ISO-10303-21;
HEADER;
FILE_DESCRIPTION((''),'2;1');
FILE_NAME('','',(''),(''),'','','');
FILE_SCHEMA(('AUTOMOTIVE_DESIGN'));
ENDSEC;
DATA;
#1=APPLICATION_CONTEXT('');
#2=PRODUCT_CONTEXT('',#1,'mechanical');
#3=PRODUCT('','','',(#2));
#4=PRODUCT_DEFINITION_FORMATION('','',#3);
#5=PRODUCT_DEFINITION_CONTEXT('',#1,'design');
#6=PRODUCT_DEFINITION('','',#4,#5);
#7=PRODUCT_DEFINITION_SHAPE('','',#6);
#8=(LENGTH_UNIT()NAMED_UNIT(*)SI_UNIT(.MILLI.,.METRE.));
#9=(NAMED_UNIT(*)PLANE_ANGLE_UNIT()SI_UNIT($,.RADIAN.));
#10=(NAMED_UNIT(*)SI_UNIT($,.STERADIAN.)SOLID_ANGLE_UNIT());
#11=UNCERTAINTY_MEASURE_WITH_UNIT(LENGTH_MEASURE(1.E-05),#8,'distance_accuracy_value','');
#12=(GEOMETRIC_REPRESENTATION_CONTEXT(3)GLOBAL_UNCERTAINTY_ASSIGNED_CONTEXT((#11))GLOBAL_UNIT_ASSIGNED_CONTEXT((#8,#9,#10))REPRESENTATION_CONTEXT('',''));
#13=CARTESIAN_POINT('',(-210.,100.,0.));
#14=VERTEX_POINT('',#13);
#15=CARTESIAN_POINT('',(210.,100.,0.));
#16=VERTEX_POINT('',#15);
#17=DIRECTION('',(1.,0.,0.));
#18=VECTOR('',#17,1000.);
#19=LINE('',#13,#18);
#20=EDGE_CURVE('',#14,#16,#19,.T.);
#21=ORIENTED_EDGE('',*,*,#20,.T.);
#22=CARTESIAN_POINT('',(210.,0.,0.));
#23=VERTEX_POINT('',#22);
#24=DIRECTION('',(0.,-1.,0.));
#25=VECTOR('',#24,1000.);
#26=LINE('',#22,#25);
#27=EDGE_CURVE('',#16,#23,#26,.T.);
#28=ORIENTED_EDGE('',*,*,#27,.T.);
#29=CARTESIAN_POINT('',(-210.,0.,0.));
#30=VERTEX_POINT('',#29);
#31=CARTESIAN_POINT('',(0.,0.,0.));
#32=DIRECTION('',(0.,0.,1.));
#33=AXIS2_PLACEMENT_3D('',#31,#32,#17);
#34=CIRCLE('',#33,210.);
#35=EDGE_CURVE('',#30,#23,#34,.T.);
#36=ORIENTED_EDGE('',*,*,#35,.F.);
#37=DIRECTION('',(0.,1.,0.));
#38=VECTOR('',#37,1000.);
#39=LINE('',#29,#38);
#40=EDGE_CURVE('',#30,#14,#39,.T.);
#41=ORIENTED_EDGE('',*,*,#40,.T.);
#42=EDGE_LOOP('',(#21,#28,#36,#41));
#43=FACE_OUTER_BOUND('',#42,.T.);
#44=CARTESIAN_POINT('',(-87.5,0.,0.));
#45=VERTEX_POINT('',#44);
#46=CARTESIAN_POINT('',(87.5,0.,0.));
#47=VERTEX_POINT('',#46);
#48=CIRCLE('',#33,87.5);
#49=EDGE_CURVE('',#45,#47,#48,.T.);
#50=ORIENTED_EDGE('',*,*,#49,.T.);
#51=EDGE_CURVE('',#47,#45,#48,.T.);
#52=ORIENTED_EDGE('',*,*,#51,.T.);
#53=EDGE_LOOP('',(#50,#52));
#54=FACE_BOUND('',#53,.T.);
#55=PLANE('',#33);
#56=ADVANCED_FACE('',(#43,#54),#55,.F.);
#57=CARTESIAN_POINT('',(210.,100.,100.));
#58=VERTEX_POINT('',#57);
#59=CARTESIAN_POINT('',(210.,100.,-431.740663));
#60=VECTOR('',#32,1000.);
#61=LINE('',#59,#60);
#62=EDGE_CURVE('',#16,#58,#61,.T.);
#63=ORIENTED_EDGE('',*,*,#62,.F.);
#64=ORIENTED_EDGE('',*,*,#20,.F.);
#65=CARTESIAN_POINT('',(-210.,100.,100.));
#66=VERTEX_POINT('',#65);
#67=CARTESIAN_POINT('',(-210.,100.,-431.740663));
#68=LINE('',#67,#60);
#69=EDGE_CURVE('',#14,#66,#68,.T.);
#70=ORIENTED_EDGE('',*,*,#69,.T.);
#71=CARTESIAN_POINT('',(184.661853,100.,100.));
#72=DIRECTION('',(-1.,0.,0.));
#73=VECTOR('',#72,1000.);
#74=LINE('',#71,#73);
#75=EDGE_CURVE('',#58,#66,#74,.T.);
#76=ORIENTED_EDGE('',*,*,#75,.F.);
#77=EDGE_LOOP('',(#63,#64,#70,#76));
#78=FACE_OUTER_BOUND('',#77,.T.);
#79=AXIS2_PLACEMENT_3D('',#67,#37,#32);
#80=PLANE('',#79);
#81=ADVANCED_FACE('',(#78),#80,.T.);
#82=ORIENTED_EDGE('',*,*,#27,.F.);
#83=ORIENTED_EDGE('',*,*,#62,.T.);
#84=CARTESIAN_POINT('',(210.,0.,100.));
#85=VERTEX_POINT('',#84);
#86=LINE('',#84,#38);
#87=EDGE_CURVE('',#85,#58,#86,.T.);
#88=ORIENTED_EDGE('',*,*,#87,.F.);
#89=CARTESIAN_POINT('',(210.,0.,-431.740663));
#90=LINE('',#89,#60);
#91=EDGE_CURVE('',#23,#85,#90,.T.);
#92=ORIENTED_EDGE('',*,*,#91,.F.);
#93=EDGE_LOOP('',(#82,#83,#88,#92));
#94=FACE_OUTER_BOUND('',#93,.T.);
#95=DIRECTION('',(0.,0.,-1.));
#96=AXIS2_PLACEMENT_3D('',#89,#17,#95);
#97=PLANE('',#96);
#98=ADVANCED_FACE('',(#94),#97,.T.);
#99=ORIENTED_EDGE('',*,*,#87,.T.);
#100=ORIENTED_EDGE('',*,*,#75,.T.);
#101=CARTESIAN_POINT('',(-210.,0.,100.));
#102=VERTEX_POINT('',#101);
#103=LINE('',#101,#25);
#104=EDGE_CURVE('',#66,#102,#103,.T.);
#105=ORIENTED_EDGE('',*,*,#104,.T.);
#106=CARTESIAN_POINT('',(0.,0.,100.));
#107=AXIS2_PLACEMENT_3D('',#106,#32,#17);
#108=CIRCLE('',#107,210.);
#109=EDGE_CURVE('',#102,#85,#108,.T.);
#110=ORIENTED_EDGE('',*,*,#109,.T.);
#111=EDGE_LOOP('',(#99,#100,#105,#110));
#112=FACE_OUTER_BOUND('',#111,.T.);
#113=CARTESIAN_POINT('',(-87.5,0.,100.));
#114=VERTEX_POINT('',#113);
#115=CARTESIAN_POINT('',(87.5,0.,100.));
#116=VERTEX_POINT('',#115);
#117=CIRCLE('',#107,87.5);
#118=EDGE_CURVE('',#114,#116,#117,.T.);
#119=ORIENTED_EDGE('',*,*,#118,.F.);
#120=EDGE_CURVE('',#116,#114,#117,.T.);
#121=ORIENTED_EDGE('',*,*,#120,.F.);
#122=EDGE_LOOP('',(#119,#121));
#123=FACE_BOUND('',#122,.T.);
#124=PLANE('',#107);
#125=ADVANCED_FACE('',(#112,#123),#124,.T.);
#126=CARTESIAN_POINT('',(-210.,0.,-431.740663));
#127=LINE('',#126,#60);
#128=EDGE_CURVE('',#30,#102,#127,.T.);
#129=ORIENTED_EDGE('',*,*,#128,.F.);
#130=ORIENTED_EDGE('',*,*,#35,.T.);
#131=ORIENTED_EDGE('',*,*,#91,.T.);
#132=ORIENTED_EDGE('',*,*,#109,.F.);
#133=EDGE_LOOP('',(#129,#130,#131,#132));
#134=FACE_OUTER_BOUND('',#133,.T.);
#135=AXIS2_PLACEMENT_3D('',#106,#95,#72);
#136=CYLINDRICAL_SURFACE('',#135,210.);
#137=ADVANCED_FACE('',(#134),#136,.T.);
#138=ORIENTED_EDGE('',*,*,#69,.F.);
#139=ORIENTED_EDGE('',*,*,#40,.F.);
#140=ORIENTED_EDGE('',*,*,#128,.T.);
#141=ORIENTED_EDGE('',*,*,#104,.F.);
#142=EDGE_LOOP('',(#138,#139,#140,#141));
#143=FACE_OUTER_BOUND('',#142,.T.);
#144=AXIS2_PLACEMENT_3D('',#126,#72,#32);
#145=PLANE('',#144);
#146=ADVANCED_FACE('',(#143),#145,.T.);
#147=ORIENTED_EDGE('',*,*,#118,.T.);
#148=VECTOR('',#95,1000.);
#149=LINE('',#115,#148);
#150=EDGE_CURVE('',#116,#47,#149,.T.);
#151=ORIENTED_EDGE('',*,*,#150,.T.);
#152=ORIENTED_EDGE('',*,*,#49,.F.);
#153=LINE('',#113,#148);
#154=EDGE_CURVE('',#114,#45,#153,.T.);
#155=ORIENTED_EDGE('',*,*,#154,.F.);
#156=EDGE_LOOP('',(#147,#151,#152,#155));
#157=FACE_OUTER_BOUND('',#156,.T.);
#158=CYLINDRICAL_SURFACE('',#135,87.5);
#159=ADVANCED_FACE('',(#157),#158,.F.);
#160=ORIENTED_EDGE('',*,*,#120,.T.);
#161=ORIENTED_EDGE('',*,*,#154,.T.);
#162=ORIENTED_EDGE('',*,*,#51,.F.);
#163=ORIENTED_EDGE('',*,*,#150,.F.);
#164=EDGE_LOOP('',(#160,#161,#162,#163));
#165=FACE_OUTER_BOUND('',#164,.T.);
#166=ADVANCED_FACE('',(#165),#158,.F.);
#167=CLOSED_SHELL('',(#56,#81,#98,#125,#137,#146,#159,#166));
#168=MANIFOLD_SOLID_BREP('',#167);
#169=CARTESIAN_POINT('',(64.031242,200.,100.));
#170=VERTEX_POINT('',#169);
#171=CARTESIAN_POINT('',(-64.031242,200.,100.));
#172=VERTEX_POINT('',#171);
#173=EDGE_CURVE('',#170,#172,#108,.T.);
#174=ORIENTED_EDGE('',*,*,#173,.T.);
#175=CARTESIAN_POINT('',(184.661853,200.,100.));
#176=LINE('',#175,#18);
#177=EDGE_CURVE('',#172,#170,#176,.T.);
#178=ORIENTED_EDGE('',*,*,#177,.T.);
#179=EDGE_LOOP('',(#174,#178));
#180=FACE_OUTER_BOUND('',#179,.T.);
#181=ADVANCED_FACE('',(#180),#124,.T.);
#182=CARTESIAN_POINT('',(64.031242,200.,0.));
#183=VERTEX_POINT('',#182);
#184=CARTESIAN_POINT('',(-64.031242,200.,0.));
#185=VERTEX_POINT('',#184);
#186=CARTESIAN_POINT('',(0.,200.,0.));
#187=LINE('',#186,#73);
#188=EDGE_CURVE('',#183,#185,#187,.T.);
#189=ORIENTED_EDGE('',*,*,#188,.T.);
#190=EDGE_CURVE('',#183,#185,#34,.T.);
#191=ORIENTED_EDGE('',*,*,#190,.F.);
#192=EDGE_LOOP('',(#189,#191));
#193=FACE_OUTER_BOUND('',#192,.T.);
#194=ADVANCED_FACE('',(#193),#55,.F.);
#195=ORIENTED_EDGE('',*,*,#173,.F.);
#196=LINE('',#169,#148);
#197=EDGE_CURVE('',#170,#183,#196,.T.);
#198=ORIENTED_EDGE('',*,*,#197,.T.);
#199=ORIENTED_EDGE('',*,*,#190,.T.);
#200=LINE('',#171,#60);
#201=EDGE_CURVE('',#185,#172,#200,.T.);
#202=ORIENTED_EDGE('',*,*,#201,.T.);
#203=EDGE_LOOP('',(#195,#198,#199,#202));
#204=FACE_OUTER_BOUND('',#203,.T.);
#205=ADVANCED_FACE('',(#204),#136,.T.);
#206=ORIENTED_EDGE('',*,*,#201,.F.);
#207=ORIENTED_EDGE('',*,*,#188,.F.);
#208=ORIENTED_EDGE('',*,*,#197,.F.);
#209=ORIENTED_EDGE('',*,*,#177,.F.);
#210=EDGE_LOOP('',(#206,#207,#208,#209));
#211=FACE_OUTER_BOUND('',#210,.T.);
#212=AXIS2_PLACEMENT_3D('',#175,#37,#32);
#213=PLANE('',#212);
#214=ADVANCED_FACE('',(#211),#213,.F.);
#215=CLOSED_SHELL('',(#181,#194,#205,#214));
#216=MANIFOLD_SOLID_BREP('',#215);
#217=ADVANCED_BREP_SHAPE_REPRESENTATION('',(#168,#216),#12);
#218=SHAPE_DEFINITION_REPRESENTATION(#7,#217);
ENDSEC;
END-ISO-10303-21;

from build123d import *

# Parameters (mm, degrees)
SKETCH1_R           = 210
SKETCH1_R_2         = 87.5
BOSS_EXTRUDE1_DEPTH = 100
BOSS_EXTRUDE2_START = -100
BOSS_EXTRUDE2_DEPTH = 100
SKETCH3_W           = 369.323706252
SKETCH3_H           = 100
CUT_EXTRUDE1_DEPTH  = 314.36879232


with BuildPart() as part:
    # Sketch1 → Boss-Extrude1 (new body)
    with BuildSketch(Plane.XY):
        Circle(SKETCH1_R)
        Circle(SKETCH1_R_2, mode=Mode.SUBTRACT)
    extrude(amount=BOSS_EXTRUDE1_DEPTH)

    # Sketch2 → Boss-Extrude2 (add)
    with BuildSketch(Plane.XY.offset(100).offset(BOSS_EXTRUDE2_START)):
        with BuildLine():
            Line((87.5, 0), (210, 0))
            Line((210, 0), (210, 100))
            Line((210, 100), (-210, 100))
            Line((-210, 100), (-210, 0))
            Line((-210, 0), (-87.5, 0))
            ThreePointArc((-87.5, 0), (0, 87.5), (87.5, 0))
        make_face()
    extrude(amount=BOSS_EXTRUDE2_DEPTH)

    # Sketch3 → Cut-Extrude1 (cut, through all)
    with BuildSketch(Plane(origin=(0, 0, 0), x_dir=(-1, 0, 0), z_dir=(0, 0, -1))):
        with Locations((0, 150)):
            Rectangle(SKETCH3_W, SKETCH3_H)
    extrude(amount=-CUT_EXTRUDE1_DEPTH, mode=Mode.SUBTRACT)


with BuildPart() as cut_extrude1_piece_1:
    # of the separate pieces the step leaves, piece 1, a body of its own (cut_extrude1_pieces)
    add(part.part.solids().sort_by_distance((-210, 100, 0))[0])


with BuildPart() as cut_extrude1_piece_2:
    # of the separate pieces the step leaves, piece 2, a body of its own (cut_extrude1_pieces)
    add(part.part.solids().sort_by_distance((64.031242374, 200, 0))[0])


solid = Compound([cut_extrude1_piece_1.part, cut_extrude1_piece_2.part])
